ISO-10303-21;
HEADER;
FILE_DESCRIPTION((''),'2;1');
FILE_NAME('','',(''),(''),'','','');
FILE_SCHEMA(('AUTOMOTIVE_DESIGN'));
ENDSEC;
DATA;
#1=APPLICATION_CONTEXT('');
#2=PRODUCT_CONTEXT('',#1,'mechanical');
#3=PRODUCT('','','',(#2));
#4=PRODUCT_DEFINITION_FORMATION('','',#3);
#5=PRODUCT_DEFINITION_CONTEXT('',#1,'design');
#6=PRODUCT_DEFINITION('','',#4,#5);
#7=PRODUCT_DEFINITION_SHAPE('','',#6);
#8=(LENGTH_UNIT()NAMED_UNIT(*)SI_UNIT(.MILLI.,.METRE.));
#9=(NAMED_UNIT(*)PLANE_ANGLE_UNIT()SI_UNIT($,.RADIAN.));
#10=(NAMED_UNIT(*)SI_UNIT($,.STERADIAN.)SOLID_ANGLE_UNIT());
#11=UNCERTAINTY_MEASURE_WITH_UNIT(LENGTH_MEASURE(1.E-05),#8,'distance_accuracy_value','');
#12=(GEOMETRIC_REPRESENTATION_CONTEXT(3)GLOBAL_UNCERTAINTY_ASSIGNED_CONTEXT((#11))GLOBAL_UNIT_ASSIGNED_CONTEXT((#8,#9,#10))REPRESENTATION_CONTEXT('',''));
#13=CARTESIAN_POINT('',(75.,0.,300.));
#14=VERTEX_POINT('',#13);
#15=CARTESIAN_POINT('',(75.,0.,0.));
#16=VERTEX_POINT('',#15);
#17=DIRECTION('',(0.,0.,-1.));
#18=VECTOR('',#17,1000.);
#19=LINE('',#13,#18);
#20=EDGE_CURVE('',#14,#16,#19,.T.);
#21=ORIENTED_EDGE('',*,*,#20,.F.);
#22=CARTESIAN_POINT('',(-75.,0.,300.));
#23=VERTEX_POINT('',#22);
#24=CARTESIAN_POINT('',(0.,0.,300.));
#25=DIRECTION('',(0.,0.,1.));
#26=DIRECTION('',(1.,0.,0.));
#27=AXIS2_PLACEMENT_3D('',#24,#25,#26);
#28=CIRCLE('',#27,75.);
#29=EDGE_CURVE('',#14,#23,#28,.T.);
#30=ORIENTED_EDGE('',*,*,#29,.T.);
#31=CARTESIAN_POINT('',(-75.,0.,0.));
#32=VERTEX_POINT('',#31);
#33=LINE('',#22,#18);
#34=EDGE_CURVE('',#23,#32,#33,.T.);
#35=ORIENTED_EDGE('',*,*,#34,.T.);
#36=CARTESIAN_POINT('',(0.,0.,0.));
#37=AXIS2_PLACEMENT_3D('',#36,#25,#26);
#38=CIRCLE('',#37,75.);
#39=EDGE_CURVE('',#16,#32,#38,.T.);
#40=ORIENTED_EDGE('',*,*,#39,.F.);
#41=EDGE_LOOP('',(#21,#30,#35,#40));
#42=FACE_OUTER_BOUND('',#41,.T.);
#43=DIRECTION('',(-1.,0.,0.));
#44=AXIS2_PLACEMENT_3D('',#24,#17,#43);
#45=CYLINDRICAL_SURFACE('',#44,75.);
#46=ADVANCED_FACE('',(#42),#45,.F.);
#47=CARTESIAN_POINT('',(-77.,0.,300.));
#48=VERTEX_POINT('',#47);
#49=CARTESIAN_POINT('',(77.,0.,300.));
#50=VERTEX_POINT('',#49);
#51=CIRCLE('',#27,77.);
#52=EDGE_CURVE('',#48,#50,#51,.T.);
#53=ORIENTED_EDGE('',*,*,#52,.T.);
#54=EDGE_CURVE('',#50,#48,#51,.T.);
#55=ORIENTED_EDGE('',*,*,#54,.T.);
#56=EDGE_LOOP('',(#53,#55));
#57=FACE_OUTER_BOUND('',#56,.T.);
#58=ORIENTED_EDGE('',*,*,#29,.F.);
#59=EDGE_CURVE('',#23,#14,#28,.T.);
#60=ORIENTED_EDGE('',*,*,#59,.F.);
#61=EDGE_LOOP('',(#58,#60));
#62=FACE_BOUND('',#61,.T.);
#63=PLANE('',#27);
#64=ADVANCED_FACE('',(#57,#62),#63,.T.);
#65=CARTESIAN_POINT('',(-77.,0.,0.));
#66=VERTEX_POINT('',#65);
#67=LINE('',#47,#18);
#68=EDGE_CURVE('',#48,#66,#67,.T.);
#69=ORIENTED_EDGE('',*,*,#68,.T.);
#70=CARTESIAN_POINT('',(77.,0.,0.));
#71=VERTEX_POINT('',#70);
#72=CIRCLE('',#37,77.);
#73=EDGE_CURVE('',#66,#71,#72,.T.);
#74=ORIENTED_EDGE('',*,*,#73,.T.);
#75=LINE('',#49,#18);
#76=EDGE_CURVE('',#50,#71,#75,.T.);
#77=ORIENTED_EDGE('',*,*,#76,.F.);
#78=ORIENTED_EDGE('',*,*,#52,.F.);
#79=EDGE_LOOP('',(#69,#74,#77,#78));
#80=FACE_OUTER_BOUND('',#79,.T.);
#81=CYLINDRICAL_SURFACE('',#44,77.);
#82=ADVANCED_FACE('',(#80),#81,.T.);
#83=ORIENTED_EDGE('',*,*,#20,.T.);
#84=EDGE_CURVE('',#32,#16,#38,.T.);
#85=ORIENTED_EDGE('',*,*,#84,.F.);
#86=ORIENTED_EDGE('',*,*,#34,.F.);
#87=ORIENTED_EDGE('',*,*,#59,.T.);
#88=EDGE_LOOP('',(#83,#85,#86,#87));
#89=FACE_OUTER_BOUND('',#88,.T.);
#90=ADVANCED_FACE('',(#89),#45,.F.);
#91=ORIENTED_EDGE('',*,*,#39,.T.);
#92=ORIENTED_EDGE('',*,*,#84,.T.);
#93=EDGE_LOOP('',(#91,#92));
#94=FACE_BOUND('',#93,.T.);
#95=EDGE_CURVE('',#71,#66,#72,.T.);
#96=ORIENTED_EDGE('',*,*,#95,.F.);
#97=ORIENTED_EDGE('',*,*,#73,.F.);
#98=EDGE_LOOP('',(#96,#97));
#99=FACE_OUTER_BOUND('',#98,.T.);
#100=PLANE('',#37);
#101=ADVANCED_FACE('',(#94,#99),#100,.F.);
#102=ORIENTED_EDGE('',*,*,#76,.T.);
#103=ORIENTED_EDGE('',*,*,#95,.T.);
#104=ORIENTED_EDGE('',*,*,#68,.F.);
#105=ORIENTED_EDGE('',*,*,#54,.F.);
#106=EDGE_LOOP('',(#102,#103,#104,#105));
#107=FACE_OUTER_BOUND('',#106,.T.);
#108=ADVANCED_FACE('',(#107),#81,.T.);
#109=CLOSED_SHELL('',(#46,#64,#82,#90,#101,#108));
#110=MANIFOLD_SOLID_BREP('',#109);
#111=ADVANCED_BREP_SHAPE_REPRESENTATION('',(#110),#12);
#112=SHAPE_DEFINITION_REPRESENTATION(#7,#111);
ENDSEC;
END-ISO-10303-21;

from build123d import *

# Parameters (mm, degrees)
SKETCH1_R           = 77
SKETCH1_R_2         = 75
BOSS_EXTRUDE1_DEPTH = 300


with BuildPart() as part:
    # Sketch1 → Boss-Extrude1 (new body)
    with BuildSketch(Plane.XY):
        Circle(SKETCH1_R)
        Circle(SKETCH1_R_2, mode=Mode.SUBTRACT)
    extrude(amount=BOSS_EXTRUDE1_DEPTH)


solid = part.part
